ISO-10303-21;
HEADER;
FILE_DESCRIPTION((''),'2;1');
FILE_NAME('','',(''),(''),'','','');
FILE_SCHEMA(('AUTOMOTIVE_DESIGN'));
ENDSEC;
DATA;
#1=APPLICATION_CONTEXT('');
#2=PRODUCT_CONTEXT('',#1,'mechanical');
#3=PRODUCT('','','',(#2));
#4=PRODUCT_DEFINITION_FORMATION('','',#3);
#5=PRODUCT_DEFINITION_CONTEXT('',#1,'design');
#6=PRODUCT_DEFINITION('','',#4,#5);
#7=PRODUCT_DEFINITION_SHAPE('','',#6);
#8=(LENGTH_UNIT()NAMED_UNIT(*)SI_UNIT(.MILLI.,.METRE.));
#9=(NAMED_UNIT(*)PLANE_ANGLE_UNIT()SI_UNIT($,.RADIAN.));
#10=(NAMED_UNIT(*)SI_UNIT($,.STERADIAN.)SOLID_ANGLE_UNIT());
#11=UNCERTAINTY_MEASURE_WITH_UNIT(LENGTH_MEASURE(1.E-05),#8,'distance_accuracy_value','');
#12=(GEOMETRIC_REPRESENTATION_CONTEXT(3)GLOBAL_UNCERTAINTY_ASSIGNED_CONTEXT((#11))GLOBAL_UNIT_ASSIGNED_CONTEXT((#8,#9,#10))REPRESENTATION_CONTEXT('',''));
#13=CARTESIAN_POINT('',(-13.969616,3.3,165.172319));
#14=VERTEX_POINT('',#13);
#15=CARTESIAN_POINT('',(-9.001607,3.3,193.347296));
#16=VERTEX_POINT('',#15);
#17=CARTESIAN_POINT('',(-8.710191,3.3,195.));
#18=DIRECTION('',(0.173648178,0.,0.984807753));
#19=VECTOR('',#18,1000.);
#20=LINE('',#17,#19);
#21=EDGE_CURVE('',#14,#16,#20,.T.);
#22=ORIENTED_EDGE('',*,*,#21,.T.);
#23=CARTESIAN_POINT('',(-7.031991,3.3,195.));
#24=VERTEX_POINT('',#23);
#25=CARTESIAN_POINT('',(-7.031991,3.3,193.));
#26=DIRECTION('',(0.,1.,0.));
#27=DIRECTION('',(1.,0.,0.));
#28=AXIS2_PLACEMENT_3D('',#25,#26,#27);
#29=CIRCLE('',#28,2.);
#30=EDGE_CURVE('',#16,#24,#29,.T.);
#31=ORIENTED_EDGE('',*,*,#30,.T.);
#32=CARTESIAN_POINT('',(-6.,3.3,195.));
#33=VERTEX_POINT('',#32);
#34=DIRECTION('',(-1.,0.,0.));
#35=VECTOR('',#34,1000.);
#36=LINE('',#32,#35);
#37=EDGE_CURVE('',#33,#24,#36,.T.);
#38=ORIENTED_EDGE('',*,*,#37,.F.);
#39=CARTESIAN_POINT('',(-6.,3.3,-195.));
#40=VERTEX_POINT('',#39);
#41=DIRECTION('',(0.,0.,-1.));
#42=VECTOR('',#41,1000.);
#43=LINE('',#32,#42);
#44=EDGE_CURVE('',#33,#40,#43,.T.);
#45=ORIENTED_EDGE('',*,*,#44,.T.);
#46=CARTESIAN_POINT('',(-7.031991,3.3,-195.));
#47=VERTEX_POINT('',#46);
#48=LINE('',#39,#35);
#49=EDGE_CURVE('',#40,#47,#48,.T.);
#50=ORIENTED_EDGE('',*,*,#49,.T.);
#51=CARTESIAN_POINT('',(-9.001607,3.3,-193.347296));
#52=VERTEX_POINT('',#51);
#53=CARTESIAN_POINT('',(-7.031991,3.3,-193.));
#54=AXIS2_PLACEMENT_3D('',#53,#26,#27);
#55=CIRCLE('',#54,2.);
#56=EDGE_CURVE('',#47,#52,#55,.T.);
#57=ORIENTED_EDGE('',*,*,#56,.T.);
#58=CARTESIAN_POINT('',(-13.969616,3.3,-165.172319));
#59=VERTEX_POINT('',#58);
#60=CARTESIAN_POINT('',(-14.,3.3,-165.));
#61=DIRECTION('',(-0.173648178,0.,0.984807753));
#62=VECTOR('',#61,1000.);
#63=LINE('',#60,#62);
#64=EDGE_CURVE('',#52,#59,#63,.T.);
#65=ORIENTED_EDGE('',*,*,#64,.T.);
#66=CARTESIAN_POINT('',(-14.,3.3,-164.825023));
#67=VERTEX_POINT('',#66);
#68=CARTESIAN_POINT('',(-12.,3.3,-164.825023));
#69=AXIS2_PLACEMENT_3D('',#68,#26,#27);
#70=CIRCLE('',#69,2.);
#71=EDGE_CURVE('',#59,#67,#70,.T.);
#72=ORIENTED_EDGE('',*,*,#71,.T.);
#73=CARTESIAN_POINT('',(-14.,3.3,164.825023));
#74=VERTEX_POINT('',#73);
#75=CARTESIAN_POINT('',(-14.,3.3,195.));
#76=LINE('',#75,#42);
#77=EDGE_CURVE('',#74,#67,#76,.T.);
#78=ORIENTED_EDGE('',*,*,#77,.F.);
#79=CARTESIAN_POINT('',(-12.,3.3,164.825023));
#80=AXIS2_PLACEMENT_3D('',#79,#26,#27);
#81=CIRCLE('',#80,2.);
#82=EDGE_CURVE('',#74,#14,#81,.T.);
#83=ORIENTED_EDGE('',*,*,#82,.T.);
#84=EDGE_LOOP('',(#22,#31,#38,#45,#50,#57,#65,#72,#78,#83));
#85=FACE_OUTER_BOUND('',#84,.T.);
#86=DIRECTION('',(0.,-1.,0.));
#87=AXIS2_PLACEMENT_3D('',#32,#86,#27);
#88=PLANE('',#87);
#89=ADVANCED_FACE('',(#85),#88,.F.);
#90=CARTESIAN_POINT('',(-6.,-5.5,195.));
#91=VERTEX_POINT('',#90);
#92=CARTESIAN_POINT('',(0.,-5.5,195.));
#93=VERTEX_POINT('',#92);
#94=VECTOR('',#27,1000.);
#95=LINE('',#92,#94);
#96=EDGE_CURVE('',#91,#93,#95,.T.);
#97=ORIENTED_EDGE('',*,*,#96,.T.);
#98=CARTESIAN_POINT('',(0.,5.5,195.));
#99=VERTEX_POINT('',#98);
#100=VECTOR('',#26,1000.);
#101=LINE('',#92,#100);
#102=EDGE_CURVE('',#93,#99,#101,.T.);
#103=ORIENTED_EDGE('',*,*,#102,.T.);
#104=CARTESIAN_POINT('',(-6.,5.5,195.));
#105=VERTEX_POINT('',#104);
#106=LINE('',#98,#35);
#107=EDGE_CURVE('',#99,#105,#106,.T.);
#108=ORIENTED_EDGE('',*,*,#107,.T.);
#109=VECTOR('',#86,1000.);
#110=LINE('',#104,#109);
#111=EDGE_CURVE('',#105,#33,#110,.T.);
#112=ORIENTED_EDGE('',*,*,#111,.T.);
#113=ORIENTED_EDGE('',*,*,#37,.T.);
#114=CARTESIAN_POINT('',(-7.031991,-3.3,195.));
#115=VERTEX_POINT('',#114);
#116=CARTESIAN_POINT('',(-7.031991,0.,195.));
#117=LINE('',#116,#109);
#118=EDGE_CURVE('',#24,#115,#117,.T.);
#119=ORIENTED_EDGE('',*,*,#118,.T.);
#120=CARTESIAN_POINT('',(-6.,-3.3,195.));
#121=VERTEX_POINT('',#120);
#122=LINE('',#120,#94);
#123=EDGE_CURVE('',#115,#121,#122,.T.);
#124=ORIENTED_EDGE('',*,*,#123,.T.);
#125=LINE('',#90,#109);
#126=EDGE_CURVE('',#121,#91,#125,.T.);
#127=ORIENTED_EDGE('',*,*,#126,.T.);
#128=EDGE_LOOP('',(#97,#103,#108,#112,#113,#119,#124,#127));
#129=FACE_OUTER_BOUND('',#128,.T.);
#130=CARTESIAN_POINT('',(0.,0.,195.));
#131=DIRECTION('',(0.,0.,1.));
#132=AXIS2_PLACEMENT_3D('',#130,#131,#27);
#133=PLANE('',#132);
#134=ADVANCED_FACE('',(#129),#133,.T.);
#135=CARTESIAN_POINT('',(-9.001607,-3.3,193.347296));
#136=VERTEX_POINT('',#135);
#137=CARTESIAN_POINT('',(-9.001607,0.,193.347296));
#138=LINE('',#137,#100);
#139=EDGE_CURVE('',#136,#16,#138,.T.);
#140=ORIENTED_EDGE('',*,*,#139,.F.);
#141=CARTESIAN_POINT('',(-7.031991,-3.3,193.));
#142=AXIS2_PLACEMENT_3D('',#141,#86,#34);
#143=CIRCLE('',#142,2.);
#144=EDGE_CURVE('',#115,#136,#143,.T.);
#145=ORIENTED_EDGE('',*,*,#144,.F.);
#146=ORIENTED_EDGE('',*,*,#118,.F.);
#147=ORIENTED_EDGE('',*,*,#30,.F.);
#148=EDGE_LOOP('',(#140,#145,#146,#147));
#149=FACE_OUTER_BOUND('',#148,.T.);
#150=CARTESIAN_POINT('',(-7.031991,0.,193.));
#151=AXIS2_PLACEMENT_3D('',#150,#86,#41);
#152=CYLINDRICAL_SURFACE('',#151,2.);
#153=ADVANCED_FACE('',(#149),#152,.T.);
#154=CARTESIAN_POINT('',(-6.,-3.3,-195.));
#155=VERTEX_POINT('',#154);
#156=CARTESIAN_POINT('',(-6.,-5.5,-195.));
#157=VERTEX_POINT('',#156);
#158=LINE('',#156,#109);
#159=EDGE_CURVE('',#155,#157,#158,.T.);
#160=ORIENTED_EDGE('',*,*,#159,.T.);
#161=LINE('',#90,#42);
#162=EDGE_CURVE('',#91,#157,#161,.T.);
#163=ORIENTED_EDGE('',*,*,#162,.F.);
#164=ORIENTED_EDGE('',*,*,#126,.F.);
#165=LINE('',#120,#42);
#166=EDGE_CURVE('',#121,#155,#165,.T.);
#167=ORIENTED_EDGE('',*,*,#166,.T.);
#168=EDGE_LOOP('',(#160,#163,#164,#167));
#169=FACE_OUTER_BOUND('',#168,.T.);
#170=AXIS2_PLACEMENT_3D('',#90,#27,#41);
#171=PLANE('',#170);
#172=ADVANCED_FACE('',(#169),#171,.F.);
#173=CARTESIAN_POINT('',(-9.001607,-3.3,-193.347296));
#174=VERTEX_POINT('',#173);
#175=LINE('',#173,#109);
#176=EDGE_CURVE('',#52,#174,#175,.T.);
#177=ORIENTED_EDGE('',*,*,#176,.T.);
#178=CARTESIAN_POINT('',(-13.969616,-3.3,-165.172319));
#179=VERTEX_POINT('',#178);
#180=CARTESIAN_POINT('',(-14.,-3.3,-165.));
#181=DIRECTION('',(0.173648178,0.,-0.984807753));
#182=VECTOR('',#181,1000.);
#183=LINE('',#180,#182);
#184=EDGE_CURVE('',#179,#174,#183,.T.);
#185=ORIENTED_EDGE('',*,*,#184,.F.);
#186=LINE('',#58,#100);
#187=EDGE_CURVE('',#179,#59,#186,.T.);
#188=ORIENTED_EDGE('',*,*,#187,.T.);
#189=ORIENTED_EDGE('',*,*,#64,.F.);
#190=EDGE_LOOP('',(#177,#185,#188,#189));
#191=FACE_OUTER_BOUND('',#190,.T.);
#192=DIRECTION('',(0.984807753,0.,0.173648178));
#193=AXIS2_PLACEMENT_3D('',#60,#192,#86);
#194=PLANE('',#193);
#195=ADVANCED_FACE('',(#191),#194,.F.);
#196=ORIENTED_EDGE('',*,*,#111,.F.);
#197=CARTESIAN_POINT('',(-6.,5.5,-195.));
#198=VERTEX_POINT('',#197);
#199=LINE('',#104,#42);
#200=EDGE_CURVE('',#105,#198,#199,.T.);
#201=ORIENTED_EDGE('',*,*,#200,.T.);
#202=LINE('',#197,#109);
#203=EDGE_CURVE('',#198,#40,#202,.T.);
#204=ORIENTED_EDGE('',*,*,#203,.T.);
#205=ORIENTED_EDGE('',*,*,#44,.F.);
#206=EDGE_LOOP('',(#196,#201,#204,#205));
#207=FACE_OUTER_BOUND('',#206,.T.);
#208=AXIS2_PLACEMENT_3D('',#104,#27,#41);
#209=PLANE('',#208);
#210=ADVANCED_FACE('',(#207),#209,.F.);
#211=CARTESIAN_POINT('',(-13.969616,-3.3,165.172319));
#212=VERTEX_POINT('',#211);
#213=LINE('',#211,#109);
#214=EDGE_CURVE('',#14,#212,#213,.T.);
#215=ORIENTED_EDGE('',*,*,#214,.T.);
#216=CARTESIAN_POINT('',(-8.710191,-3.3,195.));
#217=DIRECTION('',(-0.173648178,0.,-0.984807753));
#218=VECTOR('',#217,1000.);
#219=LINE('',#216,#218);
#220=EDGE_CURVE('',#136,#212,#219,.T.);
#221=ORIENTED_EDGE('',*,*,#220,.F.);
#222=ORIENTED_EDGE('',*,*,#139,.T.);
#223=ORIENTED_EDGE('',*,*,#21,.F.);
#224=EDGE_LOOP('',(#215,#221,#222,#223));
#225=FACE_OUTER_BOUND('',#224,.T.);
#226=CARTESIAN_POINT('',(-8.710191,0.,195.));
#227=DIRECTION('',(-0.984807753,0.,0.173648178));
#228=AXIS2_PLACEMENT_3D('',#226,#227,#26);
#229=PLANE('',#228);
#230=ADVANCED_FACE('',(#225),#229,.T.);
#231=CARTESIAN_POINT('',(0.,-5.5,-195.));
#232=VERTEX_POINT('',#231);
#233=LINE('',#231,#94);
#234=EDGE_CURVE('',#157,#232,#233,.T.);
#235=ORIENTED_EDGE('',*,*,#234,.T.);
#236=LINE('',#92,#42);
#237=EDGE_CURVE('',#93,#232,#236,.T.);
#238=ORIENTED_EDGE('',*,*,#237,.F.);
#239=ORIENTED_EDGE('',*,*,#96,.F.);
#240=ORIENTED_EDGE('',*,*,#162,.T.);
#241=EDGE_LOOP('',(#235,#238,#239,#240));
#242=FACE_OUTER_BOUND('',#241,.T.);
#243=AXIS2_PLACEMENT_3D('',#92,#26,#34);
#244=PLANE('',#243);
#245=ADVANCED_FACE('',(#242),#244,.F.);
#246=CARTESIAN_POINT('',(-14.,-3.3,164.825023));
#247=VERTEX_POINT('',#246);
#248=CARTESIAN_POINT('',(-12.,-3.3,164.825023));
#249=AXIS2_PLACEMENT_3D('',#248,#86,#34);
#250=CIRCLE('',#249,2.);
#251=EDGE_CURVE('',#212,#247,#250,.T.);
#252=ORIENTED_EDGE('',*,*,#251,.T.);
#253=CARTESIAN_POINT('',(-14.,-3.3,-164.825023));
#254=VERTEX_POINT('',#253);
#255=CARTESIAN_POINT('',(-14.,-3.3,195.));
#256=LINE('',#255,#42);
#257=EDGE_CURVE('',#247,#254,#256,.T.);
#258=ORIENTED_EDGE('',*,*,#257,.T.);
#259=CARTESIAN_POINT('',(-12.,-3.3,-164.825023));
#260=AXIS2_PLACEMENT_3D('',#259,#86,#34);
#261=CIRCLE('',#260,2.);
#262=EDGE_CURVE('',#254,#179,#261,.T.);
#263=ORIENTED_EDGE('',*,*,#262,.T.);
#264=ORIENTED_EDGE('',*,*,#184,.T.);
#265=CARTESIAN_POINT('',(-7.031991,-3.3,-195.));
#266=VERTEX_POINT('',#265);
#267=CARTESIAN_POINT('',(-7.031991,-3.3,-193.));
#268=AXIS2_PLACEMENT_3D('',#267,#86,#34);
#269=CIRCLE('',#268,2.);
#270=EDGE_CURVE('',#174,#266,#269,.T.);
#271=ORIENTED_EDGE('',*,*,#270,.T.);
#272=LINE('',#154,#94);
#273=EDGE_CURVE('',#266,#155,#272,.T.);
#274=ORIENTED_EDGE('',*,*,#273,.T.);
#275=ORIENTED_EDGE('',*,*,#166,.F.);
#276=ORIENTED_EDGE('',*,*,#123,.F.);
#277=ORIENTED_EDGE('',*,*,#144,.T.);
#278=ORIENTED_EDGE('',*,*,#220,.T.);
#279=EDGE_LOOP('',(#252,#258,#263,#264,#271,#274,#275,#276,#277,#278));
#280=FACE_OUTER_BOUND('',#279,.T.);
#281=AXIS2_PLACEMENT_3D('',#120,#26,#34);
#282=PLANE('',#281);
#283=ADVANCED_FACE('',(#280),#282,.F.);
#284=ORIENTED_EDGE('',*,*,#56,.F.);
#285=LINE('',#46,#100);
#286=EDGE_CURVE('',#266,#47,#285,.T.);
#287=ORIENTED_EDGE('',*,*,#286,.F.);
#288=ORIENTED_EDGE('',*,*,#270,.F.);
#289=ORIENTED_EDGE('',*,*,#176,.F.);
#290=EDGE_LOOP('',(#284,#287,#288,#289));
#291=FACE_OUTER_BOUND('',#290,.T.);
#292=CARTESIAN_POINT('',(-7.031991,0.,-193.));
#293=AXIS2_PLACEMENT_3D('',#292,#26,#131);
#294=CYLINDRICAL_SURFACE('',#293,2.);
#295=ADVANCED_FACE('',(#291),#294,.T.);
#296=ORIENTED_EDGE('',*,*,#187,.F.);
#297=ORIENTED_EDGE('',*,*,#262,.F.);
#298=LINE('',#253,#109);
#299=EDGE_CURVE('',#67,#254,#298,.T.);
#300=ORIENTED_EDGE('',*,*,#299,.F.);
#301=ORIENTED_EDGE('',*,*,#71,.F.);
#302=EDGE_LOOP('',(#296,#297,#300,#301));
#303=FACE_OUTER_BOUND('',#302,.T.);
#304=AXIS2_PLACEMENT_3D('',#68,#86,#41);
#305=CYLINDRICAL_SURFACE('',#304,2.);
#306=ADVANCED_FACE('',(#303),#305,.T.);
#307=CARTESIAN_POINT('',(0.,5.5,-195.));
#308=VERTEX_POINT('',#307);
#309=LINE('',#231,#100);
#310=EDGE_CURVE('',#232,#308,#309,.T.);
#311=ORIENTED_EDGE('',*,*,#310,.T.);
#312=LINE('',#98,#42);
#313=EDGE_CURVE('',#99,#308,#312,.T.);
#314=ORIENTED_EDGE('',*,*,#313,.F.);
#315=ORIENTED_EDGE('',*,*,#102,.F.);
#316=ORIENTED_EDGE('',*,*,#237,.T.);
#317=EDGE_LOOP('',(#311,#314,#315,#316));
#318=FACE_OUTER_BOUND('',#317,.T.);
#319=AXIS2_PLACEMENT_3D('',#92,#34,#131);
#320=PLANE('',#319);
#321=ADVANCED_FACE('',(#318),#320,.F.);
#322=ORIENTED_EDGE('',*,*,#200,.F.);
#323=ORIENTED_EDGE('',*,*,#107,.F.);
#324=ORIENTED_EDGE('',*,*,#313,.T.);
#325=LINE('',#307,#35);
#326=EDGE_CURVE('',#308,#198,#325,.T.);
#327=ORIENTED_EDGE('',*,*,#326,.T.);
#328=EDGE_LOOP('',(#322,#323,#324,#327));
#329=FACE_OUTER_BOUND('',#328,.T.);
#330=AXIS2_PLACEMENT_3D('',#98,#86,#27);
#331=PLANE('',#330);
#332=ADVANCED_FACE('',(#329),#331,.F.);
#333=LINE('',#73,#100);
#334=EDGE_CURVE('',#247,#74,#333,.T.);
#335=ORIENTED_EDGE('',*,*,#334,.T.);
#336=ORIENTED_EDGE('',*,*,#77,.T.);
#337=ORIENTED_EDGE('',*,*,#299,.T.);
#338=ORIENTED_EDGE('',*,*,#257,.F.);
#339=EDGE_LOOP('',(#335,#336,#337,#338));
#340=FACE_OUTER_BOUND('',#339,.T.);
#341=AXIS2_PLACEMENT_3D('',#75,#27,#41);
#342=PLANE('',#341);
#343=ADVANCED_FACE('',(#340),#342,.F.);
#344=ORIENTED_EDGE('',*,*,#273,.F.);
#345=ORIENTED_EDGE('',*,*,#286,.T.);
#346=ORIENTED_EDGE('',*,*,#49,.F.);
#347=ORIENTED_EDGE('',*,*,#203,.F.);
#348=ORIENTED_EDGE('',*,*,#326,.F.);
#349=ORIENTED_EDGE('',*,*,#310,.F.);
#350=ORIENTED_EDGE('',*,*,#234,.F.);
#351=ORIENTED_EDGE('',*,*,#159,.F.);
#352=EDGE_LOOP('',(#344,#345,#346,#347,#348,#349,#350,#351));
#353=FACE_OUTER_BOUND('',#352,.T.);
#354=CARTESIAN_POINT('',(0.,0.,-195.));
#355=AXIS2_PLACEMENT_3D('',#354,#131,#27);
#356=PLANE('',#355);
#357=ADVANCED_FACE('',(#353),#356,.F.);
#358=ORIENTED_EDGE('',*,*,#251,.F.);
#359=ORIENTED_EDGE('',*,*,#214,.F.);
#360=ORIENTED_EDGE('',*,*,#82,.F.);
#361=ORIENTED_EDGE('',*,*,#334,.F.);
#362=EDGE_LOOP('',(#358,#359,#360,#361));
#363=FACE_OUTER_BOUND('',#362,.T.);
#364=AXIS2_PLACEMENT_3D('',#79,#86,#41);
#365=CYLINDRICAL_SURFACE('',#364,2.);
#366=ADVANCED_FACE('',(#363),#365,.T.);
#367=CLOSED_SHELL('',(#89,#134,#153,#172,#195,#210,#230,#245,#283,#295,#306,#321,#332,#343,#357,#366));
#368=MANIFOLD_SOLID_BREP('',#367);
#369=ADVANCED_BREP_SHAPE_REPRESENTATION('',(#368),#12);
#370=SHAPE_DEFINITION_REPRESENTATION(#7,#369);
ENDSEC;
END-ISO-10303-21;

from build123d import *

# Parameters (mm, degrees)
BOSS_EXTRUDE1_DEPTH = 195
CHAMFER1_SIZE       = 30
CHAMFER1_SIZE2      = 5.289809421
FILLET1_R           = 2


with BuildPart() as part:
    # Sketch1 → Boss-Extrude1 (new, symmetric)
    with BuildSketch(Plane.XY):
        Polygon((0, -5.5), (0, 5.5), (-6, 5.5), (-6, 3.3), (-14, 3.3), (-14, -3.3), (-6, -3.3), (-6, -5.5), align=None)
    extrude(amount=BOSS_EXTRUDE1_DEPTH, both=True)

    # Chamfer1
    chamfer1_edges = [part.edges().sort_by_distance(p)[0] for p in [
        (-14, 0, 195),
        (-14, 0, -195),
    ]]
    chamfer1_side = [part.faces().sort_by_distance(p)[0] for p in [
        (-14, 0, 0),
    ]]
    chamfer(chamfer1_edges, length=CHAMFER1_SIZE, length2=CHAMFER1_SIZE2, reference=chamfer1_side[0])

    # Fillet1
    fillet1_edges = [part.edges().sort_by_distance(p)[0] for p in [
        (-14, 0, 165),
        (-14, 0, -165),
        (-8.710190579, 0, -195),
        (-8.710190579, 0, 195),
    ]]
    fillet(fillet1_edges, radius=FILLET1_R)


solid = part.part
